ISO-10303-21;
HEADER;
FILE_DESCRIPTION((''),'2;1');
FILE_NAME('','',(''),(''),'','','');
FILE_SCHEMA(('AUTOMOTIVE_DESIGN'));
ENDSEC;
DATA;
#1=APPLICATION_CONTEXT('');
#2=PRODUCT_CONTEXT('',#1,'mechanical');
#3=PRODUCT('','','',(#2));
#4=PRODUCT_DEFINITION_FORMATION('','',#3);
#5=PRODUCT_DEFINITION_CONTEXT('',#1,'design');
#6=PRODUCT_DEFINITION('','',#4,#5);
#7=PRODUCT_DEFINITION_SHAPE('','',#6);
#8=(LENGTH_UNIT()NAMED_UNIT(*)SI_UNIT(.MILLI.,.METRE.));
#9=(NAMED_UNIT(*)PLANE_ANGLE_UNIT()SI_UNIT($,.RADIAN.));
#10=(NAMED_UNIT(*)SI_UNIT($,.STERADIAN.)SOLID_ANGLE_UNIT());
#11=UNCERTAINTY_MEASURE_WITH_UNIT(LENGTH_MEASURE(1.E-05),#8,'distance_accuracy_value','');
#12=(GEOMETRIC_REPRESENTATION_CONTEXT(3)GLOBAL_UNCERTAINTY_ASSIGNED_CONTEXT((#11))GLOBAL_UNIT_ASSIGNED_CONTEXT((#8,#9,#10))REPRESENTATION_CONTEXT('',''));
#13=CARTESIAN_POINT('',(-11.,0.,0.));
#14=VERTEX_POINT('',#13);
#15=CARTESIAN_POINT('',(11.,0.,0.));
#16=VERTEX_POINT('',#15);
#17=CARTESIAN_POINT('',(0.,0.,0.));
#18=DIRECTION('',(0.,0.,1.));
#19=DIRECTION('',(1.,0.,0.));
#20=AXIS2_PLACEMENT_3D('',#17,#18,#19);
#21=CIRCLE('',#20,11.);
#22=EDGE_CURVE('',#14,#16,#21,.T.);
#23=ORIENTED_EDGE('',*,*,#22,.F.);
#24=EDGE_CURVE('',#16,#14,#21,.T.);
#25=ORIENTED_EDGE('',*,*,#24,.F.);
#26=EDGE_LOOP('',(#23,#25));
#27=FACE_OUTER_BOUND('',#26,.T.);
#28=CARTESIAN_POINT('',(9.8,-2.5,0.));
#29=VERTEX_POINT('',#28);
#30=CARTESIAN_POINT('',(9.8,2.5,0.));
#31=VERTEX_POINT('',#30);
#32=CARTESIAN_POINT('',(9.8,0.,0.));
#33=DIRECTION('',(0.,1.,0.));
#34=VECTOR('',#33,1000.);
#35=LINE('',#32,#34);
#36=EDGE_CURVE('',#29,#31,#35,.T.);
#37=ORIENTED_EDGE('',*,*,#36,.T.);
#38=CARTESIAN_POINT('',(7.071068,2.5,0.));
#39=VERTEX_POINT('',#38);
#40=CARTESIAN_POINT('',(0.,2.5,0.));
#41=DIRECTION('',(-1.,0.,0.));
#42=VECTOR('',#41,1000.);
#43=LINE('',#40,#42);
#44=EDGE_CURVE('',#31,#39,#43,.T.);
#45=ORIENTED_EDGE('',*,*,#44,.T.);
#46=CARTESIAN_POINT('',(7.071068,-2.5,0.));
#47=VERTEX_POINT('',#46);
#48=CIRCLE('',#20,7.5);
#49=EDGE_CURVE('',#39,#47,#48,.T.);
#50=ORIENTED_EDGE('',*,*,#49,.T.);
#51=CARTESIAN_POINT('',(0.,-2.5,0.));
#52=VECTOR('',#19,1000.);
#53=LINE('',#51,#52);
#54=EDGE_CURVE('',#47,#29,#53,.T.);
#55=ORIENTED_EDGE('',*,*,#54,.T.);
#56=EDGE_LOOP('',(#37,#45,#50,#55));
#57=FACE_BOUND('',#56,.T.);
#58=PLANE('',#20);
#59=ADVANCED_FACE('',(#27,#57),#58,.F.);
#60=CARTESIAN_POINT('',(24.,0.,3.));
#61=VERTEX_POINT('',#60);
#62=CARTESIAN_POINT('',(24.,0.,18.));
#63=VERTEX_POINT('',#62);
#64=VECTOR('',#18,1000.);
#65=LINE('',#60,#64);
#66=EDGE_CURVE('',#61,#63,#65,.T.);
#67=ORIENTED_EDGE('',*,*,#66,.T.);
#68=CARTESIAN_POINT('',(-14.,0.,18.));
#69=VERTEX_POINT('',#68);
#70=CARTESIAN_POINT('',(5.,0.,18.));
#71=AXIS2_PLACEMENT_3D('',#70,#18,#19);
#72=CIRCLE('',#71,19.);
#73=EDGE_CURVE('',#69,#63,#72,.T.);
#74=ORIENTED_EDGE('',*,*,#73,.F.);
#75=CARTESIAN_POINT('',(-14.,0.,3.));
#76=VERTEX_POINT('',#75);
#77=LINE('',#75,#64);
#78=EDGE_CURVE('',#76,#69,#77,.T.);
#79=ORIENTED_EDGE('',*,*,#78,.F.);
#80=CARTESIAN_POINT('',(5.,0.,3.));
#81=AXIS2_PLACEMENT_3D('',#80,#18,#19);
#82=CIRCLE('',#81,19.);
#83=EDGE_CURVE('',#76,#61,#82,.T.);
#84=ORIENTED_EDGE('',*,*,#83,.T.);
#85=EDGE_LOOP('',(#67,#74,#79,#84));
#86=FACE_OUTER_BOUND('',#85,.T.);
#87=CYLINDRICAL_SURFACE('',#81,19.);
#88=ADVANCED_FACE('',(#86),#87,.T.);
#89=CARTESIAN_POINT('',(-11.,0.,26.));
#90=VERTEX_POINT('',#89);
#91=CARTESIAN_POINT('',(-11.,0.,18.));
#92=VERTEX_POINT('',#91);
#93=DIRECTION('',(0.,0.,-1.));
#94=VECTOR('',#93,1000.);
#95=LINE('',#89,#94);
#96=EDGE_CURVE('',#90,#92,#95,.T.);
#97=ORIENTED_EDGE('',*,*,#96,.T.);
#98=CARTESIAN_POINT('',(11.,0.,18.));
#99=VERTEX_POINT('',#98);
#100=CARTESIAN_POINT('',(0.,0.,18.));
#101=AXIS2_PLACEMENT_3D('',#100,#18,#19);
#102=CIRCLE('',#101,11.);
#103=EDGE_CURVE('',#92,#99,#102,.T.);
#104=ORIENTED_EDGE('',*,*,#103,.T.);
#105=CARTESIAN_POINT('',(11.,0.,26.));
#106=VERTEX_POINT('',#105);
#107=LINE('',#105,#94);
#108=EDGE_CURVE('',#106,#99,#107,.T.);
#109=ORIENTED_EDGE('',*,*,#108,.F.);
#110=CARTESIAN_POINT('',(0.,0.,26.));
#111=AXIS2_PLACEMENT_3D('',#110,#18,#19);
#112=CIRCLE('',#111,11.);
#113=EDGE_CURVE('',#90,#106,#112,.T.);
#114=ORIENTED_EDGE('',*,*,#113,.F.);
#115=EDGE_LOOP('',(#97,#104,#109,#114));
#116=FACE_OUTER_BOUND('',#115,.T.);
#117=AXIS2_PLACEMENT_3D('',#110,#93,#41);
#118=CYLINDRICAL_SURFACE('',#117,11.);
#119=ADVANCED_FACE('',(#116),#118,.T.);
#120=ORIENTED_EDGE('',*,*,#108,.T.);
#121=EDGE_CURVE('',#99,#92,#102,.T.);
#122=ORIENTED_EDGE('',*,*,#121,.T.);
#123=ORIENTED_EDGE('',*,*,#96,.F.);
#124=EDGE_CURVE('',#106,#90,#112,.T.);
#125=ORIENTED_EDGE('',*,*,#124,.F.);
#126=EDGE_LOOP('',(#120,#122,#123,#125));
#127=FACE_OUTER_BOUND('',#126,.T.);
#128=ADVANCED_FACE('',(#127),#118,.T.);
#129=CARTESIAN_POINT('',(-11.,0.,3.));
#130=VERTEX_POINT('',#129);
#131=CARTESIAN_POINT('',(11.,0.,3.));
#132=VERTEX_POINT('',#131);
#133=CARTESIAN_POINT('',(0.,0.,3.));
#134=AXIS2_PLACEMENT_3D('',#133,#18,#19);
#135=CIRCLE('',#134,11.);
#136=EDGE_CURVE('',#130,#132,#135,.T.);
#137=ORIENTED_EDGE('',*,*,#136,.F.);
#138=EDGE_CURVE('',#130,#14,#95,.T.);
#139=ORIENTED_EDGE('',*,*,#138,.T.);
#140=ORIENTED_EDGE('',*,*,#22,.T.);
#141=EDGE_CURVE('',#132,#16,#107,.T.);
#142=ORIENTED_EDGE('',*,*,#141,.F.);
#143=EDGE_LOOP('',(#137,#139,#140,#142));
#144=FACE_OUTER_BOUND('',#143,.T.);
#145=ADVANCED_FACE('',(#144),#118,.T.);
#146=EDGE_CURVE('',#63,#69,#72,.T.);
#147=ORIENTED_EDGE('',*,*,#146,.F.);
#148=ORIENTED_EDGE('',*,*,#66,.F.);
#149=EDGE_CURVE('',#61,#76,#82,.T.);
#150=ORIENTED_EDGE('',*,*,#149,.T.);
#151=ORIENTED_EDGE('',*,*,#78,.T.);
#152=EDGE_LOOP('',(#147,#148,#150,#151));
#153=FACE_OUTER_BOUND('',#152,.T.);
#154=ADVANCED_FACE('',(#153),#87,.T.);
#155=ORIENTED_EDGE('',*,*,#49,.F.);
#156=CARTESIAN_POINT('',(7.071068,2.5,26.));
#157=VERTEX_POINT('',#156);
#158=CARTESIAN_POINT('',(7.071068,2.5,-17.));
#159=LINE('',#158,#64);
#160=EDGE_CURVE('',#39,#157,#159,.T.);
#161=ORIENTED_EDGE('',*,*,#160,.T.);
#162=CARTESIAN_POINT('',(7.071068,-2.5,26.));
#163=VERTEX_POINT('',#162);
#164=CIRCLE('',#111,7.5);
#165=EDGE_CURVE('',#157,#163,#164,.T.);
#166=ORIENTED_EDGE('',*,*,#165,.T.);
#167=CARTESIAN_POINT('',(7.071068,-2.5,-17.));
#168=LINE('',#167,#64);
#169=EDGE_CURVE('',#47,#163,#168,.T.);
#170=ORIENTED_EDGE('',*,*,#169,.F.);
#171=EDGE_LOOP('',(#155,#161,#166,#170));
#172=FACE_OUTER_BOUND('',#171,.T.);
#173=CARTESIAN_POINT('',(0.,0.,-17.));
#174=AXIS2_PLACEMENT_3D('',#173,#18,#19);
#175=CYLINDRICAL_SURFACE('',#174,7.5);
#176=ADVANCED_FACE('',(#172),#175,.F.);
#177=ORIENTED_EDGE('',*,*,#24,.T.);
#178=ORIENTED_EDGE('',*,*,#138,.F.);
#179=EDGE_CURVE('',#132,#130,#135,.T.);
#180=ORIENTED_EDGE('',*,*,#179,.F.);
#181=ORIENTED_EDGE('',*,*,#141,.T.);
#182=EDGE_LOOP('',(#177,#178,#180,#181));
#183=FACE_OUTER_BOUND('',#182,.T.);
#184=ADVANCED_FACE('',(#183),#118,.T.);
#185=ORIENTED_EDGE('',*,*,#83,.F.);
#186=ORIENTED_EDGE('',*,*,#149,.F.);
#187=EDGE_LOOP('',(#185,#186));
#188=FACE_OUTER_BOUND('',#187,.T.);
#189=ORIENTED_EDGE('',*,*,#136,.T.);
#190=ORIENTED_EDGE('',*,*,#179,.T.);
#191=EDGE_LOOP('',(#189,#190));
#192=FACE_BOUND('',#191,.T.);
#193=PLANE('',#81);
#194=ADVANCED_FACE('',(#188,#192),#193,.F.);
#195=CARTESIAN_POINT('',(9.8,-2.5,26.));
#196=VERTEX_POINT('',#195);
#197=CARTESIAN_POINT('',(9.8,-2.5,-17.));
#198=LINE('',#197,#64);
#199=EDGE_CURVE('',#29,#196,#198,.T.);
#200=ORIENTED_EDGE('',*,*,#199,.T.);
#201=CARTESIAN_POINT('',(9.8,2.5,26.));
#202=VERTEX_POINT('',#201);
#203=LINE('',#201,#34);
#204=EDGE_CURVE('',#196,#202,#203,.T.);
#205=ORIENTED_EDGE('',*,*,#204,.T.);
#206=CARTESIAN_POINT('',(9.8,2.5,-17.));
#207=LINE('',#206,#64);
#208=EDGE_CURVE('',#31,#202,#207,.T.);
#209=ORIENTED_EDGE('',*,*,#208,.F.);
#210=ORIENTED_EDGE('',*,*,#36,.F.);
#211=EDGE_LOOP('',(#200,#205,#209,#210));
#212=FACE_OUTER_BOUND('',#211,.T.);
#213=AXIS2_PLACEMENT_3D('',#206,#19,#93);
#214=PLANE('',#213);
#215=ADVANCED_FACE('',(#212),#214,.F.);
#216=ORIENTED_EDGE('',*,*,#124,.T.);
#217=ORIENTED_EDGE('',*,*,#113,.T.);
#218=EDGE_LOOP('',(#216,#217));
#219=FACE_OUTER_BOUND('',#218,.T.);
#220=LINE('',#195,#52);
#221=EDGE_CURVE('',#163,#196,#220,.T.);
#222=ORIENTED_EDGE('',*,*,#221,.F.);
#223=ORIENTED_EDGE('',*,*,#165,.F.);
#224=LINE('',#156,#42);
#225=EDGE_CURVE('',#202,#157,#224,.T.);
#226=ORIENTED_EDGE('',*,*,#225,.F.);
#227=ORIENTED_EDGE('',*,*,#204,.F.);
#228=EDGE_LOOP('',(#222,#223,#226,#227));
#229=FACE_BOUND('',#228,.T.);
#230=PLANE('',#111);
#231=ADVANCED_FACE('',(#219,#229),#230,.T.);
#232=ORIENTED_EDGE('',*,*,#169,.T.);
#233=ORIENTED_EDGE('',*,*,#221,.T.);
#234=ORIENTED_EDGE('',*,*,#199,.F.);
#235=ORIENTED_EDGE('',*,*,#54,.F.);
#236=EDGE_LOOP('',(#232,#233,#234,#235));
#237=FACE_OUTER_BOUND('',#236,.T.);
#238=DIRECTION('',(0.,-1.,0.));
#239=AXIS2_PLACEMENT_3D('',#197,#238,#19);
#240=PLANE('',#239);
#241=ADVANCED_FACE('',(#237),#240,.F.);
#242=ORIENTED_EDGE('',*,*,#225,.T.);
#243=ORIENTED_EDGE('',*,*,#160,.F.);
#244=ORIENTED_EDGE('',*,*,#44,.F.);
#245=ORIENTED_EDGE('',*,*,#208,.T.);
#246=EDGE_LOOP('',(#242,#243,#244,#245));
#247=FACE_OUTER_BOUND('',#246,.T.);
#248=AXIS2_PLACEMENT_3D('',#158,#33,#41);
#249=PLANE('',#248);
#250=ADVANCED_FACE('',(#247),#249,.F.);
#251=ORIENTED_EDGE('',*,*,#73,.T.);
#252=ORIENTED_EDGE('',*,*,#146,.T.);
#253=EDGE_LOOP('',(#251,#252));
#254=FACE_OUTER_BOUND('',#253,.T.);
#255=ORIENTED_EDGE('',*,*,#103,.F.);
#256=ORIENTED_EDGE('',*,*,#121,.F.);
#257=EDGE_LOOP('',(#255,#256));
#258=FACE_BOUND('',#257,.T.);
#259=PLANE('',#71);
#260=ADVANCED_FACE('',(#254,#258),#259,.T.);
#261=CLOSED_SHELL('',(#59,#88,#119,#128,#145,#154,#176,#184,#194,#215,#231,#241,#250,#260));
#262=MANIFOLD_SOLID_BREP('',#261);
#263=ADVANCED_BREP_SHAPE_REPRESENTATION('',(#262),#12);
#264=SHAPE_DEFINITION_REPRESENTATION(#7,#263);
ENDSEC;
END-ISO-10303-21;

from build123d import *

# Parameters (mm, degrees)
SKETCH1_R           = 11
BOSS_EXTRUDE1_DEPTH = 26
BOSS_EXTRUDE2_START = -8
SKETCH2_R           = 19
BOSS_EXTRUDE2_DEPTH = 15
CUT_EXTRUDE1_DEPTH  = 43


with BuildPart() as part:
    # Sketch1 → Boss-Extrude1 (new body)
    with BuildSketch(Plane.XY):
        with Locations(Location((0, 0, 0), (0, 0, 180))):
            Circle(SKETCH1_R)
    extrude(amount=BOSS_EXTRUDE1_DEPTH)

    # Sketch2 → Boss-Extrude2 (add)
    with BuildSketch(Plane.XY.offset(26).offset(BOSS_EXTRUDE2_START)):
        with Locations((5, 0)):
            Circle(SKETCH2_R)
    extrude(amount=-BOSS_EXTRUDE2_DEPTH)

    # Sketch3 → Cut-Extrude1 (cut)
    with BuildSketch(Plane.XY.offset(26)):
        with BuildLine():
            Line((7.071067812, 2.5), (9.8, 2.5))
            Line((9.8, 2.5), (9.8, -2.5))
            Line((9.8, -2.5), (7.071067812, -2.5))
            ThreePointArc((7.071067812, -2.5), (-7.5, 0), (7.071067812, 2.5))
        make_face()
    extrude(amount=-CUT_EXTRUDE1_DEPTH, mode=Mode.SUBTRACT)


solid = part.part
